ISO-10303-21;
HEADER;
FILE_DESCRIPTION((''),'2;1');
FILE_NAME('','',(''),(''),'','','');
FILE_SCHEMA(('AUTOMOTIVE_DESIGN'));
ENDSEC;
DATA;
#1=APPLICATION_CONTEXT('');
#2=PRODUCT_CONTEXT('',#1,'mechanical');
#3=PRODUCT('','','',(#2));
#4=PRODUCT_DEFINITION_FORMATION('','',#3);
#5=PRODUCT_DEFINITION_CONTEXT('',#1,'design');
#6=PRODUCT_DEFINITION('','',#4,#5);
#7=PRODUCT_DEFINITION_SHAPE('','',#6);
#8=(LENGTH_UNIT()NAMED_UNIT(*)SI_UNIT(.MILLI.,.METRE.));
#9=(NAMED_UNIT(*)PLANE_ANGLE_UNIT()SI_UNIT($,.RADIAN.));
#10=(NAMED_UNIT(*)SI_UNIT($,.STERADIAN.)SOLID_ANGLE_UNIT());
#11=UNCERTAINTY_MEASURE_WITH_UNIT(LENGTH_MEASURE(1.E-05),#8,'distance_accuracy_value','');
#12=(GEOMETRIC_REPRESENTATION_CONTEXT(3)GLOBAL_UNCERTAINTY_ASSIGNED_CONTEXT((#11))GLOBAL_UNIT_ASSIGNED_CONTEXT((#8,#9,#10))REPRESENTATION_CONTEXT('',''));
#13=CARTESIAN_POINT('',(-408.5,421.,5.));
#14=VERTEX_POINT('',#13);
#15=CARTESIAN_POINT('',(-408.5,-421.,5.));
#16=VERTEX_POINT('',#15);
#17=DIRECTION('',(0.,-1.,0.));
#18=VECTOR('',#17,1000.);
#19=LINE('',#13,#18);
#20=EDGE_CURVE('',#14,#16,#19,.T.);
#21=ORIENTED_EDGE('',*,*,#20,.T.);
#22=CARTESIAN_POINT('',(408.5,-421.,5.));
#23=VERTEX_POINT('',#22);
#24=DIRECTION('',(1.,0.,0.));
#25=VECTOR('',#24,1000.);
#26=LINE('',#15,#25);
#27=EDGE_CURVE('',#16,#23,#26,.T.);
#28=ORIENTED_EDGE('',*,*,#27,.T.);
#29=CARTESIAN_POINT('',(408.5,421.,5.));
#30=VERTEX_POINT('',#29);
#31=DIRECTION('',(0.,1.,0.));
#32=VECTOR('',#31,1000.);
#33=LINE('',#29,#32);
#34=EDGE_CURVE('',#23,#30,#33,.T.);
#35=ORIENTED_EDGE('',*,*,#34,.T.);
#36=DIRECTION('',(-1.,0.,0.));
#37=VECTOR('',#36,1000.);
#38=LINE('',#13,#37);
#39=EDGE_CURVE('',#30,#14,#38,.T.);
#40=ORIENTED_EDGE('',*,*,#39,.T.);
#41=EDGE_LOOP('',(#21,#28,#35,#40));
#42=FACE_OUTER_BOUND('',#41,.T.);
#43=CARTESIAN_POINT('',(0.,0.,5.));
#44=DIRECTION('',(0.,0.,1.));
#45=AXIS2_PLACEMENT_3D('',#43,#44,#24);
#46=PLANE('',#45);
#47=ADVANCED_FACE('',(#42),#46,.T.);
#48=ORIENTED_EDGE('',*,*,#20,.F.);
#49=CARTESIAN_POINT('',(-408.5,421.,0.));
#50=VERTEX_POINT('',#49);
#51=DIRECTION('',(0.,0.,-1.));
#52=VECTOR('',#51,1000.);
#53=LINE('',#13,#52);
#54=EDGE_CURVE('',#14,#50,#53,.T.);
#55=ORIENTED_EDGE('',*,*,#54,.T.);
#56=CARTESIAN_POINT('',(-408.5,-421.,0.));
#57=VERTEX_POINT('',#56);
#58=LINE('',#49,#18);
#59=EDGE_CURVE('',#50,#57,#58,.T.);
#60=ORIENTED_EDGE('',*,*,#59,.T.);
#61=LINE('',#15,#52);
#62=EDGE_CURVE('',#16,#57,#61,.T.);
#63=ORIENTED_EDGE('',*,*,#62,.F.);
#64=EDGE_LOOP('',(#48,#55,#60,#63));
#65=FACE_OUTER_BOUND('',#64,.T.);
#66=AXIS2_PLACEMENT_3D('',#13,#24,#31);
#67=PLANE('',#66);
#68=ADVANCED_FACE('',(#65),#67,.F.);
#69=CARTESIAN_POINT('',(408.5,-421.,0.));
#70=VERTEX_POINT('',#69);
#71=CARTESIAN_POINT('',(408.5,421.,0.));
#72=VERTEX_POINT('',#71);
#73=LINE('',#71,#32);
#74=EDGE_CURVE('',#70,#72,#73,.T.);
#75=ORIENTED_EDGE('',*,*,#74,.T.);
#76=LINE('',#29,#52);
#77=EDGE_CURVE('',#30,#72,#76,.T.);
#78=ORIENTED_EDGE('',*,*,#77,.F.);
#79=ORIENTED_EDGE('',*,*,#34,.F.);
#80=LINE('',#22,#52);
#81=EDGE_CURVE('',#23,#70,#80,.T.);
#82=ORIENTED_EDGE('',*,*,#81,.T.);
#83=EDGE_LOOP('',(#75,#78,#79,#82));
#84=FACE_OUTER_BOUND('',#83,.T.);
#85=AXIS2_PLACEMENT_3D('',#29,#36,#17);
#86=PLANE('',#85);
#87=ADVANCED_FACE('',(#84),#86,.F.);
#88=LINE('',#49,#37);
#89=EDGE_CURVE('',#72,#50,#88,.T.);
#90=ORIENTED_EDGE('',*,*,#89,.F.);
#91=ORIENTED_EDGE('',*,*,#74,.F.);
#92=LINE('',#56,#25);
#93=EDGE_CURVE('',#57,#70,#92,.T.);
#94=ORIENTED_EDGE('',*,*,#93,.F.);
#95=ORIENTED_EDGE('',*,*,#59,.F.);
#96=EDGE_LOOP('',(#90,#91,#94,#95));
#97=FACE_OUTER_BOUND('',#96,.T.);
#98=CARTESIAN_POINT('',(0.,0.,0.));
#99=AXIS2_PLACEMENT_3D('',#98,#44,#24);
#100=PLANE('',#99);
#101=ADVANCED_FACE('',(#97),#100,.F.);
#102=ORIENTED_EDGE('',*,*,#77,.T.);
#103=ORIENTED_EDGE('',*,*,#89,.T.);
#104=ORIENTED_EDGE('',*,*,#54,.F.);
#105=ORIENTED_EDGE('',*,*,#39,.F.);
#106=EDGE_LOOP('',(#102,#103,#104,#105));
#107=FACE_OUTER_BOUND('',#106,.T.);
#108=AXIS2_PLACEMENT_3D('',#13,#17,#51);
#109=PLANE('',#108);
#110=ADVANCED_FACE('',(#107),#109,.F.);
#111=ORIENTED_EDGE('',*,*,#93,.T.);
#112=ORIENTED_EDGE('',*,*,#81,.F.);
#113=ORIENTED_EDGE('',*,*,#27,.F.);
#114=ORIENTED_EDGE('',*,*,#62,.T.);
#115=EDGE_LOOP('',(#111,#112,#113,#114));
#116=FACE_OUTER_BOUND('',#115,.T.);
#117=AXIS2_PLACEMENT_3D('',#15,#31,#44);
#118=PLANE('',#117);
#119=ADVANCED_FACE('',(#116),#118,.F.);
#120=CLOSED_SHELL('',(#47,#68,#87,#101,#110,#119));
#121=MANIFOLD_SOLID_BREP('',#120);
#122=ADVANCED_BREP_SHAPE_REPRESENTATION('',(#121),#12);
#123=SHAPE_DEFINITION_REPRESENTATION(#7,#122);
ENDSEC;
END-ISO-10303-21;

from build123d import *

# Parameters (mm, degrees)
SKETCH_1_W      = 817
SKETCH_1_H      = 842
EXTRUDE_1_DEPTH = 5


with BuildPart() as part:
    # 草图1 → 凸台-拉伸1 (new body)
    with BuildSketch(Plane.XY):
        Rectangle(SKETCH_1_W, SKETCH_1_H)
    extrude(amount=EXTRUDE_1_DEPTH)


solid = part.part
